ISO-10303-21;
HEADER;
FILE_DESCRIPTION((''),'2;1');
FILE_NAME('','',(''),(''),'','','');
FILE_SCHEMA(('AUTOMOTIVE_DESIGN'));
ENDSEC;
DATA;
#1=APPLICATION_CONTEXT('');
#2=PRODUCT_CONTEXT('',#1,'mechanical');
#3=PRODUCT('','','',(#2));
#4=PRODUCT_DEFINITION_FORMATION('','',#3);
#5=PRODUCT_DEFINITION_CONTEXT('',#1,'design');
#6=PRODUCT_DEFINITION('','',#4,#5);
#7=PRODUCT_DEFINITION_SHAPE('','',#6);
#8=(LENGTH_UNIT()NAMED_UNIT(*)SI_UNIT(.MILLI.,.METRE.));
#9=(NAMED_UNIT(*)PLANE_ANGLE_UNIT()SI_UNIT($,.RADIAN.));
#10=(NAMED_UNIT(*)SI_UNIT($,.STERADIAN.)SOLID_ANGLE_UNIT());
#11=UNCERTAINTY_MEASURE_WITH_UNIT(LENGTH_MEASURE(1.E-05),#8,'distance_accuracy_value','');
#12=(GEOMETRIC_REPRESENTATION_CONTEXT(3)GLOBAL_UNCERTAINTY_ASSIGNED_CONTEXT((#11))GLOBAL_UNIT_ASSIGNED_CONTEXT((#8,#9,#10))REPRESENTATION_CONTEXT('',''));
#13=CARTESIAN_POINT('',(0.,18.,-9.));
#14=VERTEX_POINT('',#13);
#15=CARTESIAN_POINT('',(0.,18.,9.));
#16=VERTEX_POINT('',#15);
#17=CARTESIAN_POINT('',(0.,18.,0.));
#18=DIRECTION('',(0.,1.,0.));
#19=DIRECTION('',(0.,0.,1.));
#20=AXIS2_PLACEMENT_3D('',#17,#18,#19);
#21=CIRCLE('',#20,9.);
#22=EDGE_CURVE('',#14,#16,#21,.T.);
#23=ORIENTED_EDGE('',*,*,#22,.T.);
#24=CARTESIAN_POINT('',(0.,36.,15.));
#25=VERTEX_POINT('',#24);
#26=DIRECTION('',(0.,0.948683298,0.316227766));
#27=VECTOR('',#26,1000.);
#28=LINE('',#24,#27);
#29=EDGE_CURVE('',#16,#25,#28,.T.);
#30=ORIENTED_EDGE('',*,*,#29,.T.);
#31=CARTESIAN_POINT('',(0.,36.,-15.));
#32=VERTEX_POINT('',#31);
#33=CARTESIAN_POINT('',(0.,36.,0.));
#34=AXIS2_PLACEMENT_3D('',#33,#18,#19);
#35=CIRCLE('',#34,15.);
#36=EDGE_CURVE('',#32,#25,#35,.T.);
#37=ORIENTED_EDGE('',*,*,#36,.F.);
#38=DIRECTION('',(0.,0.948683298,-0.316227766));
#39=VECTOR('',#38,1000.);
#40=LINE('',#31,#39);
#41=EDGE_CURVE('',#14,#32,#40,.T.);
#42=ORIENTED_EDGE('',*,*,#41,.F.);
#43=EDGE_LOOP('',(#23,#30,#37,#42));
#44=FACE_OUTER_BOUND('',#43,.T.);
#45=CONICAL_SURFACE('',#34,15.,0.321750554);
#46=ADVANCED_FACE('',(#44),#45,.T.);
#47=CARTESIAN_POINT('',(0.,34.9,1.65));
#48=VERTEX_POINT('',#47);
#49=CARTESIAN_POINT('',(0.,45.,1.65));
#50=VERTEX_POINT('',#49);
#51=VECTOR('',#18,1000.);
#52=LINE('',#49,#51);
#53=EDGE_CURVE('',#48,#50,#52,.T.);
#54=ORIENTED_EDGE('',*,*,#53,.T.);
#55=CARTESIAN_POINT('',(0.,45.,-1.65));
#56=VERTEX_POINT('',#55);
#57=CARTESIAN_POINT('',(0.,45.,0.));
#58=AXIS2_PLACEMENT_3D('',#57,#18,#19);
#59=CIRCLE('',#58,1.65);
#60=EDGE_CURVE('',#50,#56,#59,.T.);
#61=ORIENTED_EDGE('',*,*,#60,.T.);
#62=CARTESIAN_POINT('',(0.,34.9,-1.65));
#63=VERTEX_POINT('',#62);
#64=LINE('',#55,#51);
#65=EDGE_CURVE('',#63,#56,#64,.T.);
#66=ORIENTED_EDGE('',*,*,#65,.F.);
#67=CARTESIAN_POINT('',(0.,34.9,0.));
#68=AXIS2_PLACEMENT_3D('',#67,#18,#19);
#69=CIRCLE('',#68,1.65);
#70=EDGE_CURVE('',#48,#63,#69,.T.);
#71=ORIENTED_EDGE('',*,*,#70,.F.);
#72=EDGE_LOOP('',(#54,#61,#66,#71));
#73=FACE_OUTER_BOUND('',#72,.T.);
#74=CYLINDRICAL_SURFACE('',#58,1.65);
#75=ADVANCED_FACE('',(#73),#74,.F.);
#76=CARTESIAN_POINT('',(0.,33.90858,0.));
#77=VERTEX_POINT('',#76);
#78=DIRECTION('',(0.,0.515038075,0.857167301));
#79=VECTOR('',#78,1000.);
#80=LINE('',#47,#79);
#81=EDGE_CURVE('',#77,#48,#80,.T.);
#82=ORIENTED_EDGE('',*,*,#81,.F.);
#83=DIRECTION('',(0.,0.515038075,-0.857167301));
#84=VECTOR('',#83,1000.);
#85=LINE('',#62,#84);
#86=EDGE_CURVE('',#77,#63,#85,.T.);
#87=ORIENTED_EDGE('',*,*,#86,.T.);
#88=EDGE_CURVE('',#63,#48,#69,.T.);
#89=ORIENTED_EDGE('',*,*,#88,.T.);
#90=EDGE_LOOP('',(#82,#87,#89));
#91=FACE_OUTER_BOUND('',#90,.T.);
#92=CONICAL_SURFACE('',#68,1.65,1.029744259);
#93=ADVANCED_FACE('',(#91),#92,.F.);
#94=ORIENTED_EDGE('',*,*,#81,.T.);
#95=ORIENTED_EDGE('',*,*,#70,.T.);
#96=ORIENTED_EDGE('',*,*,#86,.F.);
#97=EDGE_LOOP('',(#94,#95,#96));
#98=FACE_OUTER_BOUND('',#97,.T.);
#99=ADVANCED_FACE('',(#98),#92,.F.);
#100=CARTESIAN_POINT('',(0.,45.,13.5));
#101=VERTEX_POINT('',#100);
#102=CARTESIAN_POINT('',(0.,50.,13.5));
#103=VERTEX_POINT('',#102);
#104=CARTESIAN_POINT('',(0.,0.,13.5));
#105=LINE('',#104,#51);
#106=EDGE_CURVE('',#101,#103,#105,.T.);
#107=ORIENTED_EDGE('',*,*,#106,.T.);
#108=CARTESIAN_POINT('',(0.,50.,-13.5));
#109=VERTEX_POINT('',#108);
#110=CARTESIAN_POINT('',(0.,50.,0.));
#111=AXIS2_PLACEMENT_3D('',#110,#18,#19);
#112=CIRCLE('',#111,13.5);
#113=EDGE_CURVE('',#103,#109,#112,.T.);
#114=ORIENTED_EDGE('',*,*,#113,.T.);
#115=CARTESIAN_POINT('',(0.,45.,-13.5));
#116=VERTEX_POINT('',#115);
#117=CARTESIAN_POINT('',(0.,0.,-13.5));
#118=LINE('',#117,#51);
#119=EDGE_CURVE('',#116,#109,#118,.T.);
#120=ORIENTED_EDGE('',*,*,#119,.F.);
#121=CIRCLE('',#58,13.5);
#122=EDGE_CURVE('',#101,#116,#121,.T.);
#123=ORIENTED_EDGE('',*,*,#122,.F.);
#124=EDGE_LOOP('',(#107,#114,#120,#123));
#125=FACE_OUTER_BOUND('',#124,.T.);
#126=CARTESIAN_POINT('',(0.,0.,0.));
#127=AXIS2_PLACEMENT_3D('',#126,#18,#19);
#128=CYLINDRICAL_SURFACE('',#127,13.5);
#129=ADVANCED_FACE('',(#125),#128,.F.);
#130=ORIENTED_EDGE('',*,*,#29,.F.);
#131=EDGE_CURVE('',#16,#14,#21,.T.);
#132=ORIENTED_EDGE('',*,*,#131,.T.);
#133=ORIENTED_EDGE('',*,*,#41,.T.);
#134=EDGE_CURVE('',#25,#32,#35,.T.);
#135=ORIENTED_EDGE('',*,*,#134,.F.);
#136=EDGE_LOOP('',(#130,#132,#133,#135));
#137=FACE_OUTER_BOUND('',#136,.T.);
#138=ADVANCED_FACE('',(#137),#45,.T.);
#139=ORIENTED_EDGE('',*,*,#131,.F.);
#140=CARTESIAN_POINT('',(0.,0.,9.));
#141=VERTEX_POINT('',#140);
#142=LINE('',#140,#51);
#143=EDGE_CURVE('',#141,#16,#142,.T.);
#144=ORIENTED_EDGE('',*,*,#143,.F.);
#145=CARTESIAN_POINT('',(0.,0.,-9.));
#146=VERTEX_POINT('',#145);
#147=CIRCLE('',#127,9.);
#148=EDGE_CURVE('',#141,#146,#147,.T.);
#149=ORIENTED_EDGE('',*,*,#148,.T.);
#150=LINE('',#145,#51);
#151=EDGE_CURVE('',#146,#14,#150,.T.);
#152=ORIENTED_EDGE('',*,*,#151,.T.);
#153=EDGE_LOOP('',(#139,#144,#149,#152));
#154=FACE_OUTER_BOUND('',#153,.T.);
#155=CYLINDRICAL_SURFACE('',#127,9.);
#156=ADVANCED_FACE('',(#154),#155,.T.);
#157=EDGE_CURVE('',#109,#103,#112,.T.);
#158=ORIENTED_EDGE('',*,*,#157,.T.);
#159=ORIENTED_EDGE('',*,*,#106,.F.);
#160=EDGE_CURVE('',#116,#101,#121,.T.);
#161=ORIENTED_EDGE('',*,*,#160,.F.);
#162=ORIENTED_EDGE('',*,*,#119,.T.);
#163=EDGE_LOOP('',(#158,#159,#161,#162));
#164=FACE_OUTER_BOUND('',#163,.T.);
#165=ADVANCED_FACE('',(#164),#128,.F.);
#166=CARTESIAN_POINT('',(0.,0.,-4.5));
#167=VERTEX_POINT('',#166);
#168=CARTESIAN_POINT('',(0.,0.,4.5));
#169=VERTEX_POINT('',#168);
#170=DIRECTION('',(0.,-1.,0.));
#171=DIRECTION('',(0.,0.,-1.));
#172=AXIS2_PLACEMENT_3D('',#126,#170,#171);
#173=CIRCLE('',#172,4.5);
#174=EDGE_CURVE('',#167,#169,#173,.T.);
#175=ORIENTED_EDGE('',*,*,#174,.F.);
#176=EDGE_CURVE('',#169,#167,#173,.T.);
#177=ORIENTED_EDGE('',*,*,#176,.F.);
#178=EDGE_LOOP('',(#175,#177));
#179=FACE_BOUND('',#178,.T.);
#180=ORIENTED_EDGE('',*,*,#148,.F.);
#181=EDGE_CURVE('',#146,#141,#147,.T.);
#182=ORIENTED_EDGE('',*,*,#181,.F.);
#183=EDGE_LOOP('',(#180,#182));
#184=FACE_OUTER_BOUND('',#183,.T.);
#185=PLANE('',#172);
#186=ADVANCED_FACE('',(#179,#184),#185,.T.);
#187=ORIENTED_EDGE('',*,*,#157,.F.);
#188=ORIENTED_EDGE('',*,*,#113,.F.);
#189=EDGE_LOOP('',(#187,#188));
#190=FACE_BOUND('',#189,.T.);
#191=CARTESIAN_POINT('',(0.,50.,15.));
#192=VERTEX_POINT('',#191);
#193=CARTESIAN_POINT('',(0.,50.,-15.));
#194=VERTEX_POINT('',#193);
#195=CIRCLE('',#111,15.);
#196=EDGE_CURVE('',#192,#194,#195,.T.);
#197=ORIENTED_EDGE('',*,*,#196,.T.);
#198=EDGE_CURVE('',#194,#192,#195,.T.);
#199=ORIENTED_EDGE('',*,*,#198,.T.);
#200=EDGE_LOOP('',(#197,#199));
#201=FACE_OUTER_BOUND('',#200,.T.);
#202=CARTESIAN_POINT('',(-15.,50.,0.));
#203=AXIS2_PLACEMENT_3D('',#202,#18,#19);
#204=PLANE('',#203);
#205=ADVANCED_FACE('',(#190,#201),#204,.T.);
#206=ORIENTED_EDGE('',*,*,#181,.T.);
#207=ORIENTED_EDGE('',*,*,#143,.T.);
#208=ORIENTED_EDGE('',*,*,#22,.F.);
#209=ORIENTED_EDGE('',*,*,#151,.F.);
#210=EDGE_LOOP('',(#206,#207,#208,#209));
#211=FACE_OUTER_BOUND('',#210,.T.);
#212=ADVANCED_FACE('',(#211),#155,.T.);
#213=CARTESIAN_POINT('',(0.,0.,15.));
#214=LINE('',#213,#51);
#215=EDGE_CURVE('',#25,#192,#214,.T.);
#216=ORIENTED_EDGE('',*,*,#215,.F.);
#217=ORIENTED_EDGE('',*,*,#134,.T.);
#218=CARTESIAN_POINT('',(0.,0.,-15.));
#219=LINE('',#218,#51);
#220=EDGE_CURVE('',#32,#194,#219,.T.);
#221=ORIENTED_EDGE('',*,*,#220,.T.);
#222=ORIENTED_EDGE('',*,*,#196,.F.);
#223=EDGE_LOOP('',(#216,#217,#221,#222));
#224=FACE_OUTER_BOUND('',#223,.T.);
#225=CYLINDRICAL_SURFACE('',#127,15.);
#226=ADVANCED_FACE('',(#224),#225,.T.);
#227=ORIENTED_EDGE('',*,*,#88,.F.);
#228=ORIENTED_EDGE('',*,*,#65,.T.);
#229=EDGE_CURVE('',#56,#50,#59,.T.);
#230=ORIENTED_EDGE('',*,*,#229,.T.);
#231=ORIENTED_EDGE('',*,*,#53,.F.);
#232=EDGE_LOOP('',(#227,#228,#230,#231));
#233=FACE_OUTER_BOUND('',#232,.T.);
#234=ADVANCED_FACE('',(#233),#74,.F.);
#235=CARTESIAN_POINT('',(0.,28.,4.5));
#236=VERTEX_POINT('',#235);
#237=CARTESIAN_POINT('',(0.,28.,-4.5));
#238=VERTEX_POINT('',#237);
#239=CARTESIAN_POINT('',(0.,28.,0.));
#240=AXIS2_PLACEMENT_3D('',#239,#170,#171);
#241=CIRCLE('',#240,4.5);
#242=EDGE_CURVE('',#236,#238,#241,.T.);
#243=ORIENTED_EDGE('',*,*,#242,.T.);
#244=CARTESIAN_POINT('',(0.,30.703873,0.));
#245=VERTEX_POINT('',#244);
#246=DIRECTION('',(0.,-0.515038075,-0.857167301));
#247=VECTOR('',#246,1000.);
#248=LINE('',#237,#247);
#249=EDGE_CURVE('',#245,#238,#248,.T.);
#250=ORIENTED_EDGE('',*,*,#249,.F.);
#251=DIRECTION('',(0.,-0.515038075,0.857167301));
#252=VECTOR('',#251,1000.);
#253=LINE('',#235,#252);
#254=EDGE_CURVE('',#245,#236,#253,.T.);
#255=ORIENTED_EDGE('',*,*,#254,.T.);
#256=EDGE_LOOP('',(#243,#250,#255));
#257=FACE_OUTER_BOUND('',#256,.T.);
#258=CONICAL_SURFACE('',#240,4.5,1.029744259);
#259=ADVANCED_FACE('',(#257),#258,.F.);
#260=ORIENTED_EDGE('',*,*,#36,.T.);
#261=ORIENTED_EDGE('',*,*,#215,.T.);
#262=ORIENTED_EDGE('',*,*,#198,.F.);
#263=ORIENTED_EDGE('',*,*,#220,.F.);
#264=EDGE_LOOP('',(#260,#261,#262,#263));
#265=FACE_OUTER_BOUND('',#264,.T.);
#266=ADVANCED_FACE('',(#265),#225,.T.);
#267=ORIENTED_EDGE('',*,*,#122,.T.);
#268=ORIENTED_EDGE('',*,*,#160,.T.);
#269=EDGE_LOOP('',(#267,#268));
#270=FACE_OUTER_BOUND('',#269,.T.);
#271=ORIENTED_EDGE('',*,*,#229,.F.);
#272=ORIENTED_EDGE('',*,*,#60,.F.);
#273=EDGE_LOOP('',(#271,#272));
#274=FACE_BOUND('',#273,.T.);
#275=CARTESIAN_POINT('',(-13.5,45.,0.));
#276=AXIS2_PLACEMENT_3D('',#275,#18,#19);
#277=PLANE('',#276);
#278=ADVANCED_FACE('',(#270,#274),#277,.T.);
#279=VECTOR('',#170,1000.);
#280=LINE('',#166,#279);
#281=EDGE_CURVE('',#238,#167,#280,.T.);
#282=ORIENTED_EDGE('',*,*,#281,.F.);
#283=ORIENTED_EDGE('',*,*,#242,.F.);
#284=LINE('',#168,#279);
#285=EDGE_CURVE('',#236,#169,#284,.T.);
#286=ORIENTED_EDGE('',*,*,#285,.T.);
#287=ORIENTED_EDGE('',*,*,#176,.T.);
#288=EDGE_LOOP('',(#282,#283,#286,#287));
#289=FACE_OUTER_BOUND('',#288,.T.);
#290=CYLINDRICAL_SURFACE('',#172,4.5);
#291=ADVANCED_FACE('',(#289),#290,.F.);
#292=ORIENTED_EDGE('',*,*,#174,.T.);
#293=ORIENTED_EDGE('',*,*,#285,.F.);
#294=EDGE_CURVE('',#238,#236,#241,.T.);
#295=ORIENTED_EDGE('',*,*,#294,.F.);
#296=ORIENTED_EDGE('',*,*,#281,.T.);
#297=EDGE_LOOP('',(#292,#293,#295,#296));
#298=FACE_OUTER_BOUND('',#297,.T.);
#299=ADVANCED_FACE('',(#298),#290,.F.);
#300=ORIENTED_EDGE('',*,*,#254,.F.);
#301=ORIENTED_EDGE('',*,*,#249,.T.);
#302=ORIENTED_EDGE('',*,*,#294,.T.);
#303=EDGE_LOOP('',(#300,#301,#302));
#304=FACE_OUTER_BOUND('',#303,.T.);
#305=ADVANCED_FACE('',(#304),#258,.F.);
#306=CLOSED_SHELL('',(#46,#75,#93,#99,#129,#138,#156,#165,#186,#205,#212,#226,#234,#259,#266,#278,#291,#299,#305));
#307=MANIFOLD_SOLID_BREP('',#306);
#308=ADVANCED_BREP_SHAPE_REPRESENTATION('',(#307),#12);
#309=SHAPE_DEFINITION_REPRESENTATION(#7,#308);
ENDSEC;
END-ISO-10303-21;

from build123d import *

# Parameters (mm, degrees)
M10X1_0_TAPPED_HOLE1_D     = 9
M10X1_0_TAPPED_HOLE1_DEPTH = 28
M10X1_0_TAPPED_HOLE1_TIP   = 2.703872786
M4_TAPPED_HOLE1_D          = 3.3
M4_TAPPED_HOLE1_DEPTH      = 10.1
M4_TAPPED_HOLE1_TIP        = 0.991420021


with BuildPart() as part:
    # Sketch1 → Revolve1 (revolve)
    with BuildSketch(Plane.XY, mode=Mode.PRIVATE) as revolve1_sk:
        Polygon((0, 0), (-9, 0), (-9, 18), (-15, 36), (-15, 50), (-13.5, 50), (-13.5, 45), (0, 45), align=None)
    revolve(revolve1_sk.sketch.rotate(Axis((0, 0, 0), (0, -1, 0)), 270), axis=Axis((0, 0, 0), (0, -1, 0)))

    # M10x1.0 Tapped Hole1
    with Locations(Plane(origin=(0, 0, 0), x_dir=(-1, 0, 0), z_dir=(0, -1, 0))):
        with Locations((0, 0)):
            Hole(M10X1_0_TAPPED_HOLE1_D / 2, depth=M10X1_0_TAPPED_HOLE1_DEPTH)
            with Locations((0, 0, -(M10X1_0_TAPPED_HOLE1_DEPTH + M10X1_0_TAPPED_HOLE1_TIP / 2))):  # 118° drill point
                Cone(0, M10X1_0_TAPPED_HOLE1_D / 2, M10X1_0_TAPPED_HOLE1_TIP, mode=Mode.SUBTRACT)

    # M4 Tapped Hole1
    with Locations(Plane(origin=(0, 45, 0), x_dir=(1, 0, 0), z_dir=(0, 1, 0))):
        with Locations((0, 0)):
            Hole(M4_TAPPED_HOLE1_D / 2, depth=M4_TAPPED_HOLE1_DEPTH)
            with Locations((0, 0, -(M4_TAPPED_HOLE1_DEPTH + M4_TAPPED_HOLE1_TIP / 2))):  # 118° drill point
                Cone(0, M4_TAPPED_HOLE1_D / 2, M4_TAPPED_HOLE1_TIP, mode=Mode.SUBTRACT)


solid = part.part
